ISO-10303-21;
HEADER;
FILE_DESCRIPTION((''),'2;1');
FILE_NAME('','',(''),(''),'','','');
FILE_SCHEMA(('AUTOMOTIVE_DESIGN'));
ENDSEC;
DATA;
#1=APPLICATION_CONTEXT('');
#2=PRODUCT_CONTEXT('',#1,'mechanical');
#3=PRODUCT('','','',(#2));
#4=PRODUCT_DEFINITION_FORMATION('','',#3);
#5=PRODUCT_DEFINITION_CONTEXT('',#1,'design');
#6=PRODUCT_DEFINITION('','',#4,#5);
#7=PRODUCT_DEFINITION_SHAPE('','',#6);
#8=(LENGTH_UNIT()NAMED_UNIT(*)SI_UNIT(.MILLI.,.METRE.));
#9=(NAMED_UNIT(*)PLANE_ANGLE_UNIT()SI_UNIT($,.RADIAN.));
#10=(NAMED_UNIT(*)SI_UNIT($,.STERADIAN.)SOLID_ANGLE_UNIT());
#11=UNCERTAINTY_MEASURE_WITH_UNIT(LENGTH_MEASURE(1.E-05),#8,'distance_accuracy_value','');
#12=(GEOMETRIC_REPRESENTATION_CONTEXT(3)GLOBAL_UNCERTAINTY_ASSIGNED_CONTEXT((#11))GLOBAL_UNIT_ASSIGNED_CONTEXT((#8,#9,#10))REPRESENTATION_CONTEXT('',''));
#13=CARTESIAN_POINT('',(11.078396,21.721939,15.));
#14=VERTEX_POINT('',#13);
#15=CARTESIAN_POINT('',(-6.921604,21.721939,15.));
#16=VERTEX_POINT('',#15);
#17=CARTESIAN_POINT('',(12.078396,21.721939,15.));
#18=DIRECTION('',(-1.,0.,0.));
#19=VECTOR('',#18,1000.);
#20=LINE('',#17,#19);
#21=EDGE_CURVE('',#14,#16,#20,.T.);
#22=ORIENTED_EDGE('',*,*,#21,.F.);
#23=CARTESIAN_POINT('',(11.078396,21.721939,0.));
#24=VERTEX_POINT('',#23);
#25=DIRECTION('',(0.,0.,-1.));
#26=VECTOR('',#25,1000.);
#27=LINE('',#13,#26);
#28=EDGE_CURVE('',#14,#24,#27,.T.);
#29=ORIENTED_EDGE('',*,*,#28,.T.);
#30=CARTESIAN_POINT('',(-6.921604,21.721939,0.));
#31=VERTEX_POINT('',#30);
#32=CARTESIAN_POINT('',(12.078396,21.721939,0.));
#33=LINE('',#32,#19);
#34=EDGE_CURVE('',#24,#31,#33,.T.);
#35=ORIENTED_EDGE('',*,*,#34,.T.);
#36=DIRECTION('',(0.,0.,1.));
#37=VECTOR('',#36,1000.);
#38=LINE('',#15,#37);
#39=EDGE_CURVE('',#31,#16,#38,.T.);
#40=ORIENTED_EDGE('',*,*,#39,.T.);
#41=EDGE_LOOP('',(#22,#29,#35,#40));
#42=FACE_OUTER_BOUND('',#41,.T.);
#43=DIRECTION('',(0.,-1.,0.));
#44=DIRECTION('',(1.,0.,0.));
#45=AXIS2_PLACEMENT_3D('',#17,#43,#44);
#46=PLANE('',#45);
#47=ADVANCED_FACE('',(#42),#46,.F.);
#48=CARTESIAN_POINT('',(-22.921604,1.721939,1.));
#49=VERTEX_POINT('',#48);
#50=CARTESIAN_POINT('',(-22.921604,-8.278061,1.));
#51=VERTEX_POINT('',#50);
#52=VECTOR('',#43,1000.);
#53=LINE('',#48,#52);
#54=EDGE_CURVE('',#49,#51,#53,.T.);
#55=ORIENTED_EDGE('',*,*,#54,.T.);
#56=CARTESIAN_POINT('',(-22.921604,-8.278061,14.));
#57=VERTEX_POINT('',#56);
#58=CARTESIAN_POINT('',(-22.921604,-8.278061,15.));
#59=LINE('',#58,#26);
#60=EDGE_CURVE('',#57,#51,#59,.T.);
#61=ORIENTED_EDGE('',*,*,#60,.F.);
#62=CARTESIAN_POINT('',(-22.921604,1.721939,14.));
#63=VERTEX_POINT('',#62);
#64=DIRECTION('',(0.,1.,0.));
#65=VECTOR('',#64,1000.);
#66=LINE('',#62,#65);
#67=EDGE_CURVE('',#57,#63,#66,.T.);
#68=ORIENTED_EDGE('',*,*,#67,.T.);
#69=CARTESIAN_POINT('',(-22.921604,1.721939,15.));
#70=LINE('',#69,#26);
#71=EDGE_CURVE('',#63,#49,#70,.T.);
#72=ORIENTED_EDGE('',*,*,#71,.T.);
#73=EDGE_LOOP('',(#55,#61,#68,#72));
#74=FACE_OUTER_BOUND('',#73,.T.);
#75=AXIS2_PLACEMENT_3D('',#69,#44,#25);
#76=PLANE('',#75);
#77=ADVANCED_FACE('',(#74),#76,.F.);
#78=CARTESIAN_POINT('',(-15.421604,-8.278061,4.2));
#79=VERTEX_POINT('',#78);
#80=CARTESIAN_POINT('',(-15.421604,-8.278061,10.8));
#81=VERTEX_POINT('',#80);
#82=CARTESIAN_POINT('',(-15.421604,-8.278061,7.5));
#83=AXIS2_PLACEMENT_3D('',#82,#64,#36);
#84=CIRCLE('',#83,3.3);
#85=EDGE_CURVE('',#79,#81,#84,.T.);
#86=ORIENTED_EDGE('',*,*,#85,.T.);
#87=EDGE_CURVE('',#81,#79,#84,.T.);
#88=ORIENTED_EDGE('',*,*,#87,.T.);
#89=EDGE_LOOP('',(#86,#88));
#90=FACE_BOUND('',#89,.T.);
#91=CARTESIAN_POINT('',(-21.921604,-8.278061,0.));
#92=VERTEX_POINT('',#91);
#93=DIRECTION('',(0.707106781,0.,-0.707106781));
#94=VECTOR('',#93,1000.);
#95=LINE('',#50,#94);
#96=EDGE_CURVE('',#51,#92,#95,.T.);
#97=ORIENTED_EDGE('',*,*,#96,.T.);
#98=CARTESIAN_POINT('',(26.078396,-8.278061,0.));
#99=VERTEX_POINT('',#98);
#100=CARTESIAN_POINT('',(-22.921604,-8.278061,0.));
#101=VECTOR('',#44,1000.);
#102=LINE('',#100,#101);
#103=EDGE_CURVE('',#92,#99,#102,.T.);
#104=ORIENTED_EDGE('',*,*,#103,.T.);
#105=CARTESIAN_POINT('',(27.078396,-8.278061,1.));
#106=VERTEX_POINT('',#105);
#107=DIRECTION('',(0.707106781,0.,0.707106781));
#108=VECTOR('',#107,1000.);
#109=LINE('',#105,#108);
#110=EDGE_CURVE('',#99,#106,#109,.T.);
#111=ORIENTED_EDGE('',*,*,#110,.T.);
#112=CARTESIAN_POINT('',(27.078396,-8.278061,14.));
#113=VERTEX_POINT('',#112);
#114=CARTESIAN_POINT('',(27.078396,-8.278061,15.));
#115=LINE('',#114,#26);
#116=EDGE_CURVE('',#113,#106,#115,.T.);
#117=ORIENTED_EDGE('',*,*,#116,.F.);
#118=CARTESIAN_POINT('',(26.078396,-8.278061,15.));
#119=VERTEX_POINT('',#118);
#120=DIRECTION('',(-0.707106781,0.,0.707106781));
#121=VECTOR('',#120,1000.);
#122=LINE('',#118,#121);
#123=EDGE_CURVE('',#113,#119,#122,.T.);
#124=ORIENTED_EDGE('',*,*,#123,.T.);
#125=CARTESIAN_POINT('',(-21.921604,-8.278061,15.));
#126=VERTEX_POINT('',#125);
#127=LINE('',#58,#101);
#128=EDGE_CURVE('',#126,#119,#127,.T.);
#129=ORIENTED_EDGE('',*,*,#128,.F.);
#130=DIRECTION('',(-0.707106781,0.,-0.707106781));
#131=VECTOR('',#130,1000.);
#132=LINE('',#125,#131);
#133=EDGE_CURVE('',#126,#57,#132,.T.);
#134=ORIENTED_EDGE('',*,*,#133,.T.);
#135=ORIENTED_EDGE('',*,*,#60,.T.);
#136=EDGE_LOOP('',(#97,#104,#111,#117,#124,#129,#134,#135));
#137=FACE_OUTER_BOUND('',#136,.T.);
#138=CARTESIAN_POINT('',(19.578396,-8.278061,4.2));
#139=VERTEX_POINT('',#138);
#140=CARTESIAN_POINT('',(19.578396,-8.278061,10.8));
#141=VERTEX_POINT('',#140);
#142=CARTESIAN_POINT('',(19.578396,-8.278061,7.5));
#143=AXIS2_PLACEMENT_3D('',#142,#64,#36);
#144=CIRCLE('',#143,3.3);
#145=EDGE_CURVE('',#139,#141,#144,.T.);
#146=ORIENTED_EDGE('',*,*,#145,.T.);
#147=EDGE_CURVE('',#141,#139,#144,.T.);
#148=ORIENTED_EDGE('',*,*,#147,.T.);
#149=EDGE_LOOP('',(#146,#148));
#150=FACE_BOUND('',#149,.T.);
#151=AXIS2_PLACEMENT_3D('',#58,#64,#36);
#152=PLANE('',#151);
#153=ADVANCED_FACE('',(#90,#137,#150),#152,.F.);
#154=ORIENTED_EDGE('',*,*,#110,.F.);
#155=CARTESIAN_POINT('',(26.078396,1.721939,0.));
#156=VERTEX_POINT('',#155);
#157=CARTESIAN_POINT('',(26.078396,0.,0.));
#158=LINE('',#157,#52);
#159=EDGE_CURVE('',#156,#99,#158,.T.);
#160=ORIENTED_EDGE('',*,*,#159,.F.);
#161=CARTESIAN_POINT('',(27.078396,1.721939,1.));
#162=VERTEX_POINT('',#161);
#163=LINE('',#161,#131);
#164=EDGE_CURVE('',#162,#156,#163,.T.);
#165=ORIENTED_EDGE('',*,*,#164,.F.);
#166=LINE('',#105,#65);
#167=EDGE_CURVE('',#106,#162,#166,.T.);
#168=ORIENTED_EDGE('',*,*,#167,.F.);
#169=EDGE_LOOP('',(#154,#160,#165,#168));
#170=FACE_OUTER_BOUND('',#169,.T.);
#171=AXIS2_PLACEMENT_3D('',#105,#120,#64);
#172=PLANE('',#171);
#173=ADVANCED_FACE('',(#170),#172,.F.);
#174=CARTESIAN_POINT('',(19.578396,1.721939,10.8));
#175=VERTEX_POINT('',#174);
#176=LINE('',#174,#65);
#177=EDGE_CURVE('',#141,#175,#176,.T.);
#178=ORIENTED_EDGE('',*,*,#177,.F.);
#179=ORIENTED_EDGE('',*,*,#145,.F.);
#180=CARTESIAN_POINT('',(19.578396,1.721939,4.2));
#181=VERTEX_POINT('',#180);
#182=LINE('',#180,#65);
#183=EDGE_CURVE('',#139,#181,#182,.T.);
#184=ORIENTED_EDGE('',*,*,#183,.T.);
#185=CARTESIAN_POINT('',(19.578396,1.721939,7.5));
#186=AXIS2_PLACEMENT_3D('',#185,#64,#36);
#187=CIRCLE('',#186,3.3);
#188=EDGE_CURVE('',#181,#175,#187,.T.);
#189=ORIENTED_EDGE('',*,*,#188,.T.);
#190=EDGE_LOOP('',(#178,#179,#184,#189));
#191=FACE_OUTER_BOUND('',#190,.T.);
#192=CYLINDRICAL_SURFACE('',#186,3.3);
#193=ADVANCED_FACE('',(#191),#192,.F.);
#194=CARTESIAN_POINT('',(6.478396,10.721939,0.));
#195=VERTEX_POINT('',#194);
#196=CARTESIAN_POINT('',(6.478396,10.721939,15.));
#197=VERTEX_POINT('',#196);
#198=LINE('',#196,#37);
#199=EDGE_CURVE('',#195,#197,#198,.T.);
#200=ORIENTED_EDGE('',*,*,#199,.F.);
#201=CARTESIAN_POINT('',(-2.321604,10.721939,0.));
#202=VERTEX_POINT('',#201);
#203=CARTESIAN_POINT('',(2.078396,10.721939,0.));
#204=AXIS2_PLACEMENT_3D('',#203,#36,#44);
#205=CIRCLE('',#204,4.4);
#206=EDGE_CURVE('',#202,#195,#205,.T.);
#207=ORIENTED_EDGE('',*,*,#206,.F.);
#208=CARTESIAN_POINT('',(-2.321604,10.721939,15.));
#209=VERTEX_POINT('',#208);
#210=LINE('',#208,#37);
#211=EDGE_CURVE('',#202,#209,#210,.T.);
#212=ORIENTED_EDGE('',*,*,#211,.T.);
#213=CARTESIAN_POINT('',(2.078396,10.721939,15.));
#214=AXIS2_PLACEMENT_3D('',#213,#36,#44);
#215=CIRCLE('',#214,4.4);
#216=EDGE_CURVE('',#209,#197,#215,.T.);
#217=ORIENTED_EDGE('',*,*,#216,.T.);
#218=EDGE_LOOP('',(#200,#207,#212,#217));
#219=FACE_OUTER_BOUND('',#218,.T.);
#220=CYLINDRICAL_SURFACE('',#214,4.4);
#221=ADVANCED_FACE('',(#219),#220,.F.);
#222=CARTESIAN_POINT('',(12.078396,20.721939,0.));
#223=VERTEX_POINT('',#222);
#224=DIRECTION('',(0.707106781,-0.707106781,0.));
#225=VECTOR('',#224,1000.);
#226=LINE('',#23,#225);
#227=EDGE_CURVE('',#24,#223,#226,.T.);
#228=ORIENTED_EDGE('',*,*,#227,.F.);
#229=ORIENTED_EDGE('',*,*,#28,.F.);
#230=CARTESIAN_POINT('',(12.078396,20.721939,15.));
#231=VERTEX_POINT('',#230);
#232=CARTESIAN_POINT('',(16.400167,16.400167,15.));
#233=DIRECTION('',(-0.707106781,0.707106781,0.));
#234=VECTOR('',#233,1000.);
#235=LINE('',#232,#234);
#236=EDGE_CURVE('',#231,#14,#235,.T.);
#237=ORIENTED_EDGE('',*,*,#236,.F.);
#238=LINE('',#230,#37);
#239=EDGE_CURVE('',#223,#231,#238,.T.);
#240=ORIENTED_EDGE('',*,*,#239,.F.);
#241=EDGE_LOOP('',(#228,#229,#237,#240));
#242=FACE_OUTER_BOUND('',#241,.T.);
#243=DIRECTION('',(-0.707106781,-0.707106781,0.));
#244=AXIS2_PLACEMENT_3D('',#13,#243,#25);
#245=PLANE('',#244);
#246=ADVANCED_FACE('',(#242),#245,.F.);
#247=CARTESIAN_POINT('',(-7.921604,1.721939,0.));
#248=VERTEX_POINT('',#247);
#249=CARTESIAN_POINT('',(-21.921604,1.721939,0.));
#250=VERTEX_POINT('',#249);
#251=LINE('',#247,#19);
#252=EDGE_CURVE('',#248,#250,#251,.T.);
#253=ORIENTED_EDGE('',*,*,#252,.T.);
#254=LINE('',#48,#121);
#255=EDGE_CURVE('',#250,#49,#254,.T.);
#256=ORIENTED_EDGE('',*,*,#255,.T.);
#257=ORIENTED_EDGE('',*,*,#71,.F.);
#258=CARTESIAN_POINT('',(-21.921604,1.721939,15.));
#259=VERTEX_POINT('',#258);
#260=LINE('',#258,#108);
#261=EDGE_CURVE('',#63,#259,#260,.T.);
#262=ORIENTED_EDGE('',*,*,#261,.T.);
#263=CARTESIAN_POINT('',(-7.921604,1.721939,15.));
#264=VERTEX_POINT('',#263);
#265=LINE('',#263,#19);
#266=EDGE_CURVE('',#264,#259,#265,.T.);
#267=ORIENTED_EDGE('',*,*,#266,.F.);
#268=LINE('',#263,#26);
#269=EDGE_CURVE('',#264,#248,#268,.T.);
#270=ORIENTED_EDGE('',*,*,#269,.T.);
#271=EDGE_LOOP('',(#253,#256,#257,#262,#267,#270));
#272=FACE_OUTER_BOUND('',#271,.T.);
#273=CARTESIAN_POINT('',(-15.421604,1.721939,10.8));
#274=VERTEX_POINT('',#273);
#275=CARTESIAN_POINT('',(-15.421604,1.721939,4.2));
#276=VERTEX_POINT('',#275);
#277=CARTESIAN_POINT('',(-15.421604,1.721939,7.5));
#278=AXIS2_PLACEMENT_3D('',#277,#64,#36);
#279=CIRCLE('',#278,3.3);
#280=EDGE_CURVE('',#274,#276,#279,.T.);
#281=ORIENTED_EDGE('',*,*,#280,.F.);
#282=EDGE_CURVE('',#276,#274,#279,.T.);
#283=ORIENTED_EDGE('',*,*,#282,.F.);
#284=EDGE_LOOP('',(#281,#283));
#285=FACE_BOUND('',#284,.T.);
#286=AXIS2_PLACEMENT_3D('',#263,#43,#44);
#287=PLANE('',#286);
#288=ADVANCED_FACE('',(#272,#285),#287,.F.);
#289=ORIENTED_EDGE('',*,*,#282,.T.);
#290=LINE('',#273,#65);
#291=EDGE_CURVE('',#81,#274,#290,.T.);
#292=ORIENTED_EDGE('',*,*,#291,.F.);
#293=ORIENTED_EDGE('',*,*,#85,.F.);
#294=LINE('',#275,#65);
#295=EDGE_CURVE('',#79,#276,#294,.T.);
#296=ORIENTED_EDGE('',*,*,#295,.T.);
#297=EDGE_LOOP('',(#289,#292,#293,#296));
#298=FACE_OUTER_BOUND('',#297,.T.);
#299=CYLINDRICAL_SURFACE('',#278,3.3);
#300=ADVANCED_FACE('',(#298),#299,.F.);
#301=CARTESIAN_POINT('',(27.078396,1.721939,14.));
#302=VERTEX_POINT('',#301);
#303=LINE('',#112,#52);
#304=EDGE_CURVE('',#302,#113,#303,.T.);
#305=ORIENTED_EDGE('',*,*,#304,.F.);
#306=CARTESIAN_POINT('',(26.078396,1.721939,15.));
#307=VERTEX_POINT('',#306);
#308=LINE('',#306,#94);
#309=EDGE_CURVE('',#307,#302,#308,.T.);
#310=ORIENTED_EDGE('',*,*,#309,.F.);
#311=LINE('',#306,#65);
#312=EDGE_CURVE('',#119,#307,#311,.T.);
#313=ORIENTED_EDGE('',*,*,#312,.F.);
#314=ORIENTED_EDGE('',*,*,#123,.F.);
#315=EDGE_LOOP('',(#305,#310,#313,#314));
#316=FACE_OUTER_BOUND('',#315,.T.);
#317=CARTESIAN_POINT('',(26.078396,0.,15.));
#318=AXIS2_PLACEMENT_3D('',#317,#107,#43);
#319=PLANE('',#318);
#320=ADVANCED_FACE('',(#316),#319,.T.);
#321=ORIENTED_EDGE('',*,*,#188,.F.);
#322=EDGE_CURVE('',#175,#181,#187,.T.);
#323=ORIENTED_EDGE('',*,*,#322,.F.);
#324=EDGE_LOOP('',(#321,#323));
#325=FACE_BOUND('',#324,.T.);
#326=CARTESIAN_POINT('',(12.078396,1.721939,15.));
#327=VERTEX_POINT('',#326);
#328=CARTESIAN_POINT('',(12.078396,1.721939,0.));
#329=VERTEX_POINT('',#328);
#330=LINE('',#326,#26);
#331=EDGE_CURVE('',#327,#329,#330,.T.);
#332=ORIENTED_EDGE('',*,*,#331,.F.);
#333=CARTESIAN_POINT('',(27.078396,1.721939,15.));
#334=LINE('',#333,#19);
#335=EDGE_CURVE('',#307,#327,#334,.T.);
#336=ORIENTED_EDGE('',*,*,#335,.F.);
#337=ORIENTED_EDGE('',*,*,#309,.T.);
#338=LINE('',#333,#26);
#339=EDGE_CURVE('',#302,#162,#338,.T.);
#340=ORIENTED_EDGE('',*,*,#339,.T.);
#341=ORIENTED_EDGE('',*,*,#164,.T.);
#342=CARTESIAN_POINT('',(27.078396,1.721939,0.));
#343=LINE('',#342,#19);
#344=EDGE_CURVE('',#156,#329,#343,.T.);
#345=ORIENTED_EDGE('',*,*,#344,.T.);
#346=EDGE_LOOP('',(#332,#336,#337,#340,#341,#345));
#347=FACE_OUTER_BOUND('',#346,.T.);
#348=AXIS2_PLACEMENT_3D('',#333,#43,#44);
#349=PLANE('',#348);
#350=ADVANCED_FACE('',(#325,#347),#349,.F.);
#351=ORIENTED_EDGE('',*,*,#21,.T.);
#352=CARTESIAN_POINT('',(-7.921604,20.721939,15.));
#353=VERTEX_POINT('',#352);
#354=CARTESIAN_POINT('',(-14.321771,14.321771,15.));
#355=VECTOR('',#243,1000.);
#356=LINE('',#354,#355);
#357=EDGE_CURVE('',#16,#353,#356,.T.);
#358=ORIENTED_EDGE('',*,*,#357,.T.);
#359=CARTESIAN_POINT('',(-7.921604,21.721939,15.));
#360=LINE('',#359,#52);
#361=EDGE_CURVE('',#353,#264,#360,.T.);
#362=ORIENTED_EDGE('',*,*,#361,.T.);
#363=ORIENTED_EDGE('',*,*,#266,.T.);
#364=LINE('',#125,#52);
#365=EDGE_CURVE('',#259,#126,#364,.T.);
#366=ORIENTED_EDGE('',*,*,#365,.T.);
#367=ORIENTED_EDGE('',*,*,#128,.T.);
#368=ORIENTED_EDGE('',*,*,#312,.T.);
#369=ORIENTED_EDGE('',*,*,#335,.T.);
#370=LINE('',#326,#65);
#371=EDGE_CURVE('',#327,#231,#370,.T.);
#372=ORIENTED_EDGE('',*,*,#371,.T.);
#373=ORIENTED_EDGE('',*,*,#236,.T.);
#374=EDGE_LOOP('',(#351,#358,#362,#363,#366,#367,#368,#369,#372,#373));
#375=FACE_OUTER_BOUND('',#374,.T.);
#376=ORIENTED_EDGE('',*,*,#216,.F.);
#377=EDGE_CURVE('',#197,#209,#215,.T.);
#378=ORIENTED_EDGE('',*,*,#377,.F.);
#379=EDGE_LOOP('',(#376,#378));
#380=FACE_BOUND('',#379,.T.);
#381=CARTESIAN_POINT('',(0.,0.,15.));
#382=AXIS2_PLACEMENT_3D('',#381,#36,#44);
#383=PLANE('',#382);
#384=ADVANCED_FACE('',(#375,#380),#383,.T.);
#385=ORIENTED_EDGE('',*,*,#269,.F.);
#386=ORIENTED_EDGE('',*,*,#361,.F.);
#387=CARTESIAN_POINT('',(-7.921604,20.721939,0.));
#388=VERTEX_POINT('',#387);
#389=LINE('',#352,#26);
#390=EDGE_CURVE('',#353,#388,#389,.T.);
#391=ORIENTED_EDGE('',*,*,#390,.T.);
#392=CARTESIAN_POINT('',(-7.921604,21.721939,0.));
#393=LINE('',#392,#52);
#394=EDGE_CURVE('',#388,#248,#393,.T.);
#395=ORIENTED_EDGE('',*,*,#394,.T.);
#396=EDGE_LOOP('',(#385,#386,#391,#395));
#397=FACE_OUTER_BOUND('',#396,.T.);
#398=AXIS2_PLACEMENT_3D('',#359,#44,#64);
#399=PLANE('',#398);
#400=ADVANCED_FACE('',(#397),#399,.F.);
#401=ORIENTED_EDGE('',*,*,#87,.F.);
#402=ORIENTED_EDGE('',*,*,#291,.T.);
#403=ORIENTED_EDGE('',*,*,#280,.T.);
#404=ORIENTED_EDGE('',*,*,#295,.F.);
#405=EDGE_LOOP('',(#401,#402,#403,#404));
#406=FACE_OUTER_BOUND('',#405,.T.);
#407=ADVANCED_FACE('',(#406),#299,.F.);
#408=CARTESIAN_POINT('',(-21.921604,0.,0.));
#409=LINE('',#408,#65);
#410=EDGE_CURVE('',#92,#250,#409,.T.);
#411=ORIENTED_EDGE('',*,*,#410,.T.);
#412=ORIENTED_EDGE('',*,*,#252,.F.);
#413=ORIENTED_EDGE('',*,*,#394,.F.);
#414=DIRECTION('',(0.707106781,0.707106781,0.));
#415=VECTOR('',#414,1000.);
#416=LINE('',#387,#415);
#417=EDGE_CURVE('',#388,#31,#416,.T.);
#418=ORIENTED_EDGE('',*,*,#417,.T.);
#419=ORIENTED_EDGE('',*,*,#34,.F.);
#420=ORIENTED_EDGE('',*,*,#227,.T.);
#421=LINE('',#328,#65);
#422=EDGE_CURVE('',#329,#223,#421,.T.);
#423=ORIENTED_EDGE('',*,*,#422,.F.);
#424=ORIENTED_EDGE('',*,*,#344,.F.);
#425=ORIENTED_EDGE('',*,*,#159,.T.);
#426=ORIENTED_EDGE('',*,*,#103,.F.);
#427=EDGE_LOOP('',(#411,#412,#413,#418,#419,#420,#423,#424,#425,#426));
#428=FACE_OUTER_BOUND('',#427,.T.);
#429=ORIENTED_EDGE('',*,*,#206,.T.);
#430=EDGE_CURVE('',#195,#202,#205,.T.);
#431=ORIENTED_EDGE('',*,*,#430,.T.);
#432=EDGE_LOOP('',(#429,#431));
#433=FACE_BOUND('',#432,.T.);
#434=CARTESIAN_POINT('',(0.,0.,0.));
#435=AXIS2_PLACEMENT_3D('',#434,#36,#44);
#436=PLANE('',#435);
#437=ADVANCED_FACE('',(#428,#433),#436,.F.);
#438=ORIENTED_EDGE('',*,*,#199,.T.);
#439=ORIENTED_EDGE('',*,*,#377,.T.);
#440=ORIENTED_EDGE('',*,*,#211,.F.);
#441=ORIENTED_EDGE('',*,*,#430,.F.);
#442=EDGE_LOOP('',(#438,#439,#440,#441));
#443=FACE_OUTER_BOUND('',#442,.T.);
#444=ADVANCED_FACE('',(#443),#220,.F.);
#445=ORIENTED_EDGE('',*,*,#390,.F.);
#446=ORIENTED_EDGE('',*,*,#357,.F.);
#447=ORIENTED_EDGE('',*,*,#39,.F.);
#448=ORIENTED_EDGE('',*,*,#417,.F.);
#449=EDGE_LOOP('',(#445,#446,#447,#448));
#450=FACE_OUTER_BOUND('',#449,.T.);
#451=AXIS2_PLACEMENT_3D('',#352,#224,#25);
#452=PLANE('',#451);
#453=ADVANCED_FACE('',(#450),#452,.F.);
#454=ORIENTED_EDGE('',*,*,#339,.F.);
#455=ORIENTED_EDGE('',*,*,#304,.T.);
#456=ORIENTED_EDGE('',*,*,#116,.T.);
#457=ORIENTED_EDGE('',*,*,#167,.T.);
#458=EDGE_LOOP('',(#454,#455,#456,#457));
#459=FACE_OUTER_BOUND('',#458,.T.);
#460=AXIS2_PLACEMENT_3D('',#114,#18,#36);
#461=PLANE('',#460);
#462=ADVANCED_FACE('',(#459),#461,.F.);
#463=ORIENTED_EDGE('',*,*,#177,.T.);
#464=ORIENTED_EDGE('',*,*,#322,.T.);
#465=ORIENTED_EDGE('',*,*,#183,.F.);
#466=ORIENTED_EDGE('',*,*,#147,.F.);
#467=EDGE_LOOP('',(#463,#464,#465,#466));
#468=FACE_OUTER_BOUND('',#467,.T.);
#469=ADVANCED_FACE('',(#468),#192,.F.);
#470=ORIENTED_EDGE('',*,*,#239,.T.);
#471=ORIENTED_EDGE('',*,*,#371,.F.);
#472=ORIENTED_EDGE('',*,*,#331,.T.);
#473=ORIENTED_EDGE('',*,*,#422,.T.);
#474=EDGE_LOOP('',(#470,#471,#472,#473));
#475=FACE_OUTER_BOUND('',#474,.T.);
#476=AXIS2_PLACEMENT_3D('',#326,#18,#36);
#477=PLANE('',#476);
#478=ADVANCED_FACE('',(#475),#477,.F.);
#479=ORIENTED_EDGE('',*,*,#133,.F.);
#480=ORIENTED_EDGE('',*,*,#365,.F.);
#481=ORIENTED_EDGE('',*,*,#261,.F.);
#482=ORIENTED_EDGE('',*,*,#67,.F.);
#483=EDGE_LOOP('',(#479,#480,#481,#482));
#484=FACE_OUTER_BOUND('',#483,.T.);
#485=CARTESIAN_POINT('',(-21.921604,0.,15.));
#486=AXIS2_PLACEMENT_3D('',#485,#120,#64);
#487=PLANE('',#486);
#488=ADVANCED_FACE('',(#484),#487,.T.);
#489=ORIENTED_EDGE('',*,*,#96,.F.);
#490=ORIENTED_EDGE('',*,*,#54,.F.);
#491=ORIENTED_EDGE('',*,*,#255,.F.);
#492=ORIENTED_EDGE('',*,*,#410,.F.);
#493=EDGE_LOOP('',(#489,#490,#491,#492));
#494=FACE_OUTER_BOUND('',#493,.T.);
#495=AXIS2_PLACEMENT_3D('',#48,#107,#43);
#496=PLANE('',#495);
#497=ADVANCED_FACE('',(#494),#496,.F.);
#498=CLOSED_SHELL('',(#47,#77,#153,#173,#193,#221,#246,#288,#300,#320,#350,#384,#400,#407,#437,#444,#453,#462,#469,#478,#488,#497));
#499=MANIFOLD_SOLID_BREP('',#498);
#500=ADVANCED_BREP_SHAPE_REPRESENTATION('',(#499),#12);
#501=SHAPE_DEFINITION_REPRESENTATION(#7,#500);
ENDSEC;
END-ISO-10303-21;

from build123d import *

# Parameters (mm, degrees)
BOSS_EXTRUDE1_DEPTH     = 15
CHAMFER1_SIZE           = 1
HOLE1_D                 = 6.6
M10X1_25_TAPPED_HOLE1_D = 8.8


with BuildPart() as part:
    # Sketch1 → Boss-Extrude1 (new body)
    with BuildSketch(Plane.XY):
        Polygon((-7.92160415, 21.721938776), (-7.92160415, 1.721938776), (-22.92160415, 1.721938776), (-22.92160415, -8.278061224), (27.07839585, -8.278061224), (27.07839585, 1.721938776), (12.07839585, 1.721938776), (12.07839585, 21.721938776), align=None)
    extrude(amount=BOSS_EXTRUDE1_DEPTH)

    # Chamfer1
    chamfer1_edges = [part.edges().sort_by_distance(p)[0] for p in [
        (-22.92160415, -3.278061224, 0),
        (12.07839585, 21.721938776, 7.5),
        (-7.92160415, 21.721938776, 7.5),
        (-22.92160415, -3.278061224, 15),
        (27.07839585, -3.278061224, 15),
        (27.07839585, -3.278061224, 0),
    ]]
    chamfer(chamfer1_edges, length=CHAMFER1_SIZE)

    # Hole1 (through all)
    with Locations(Plane(origin=(0, 1.721938776, 0), x_dir=(1, 0, 0), z_dir=(0, 1, 0))):
        with Locations((-15.42160415, -7.5), (19.57839585, -7.5)):
            Hole(HOLE1_D / 2)

    # M10x1.25 Tapped Hole1 (through all)
    with Locations(Plane.XY.offset(15)):
        with Locations((2.07839585, 10.721938776)):
            Hole(M10X1_25_TAPPED_HOLE1_D / 2)


solid = part.part
